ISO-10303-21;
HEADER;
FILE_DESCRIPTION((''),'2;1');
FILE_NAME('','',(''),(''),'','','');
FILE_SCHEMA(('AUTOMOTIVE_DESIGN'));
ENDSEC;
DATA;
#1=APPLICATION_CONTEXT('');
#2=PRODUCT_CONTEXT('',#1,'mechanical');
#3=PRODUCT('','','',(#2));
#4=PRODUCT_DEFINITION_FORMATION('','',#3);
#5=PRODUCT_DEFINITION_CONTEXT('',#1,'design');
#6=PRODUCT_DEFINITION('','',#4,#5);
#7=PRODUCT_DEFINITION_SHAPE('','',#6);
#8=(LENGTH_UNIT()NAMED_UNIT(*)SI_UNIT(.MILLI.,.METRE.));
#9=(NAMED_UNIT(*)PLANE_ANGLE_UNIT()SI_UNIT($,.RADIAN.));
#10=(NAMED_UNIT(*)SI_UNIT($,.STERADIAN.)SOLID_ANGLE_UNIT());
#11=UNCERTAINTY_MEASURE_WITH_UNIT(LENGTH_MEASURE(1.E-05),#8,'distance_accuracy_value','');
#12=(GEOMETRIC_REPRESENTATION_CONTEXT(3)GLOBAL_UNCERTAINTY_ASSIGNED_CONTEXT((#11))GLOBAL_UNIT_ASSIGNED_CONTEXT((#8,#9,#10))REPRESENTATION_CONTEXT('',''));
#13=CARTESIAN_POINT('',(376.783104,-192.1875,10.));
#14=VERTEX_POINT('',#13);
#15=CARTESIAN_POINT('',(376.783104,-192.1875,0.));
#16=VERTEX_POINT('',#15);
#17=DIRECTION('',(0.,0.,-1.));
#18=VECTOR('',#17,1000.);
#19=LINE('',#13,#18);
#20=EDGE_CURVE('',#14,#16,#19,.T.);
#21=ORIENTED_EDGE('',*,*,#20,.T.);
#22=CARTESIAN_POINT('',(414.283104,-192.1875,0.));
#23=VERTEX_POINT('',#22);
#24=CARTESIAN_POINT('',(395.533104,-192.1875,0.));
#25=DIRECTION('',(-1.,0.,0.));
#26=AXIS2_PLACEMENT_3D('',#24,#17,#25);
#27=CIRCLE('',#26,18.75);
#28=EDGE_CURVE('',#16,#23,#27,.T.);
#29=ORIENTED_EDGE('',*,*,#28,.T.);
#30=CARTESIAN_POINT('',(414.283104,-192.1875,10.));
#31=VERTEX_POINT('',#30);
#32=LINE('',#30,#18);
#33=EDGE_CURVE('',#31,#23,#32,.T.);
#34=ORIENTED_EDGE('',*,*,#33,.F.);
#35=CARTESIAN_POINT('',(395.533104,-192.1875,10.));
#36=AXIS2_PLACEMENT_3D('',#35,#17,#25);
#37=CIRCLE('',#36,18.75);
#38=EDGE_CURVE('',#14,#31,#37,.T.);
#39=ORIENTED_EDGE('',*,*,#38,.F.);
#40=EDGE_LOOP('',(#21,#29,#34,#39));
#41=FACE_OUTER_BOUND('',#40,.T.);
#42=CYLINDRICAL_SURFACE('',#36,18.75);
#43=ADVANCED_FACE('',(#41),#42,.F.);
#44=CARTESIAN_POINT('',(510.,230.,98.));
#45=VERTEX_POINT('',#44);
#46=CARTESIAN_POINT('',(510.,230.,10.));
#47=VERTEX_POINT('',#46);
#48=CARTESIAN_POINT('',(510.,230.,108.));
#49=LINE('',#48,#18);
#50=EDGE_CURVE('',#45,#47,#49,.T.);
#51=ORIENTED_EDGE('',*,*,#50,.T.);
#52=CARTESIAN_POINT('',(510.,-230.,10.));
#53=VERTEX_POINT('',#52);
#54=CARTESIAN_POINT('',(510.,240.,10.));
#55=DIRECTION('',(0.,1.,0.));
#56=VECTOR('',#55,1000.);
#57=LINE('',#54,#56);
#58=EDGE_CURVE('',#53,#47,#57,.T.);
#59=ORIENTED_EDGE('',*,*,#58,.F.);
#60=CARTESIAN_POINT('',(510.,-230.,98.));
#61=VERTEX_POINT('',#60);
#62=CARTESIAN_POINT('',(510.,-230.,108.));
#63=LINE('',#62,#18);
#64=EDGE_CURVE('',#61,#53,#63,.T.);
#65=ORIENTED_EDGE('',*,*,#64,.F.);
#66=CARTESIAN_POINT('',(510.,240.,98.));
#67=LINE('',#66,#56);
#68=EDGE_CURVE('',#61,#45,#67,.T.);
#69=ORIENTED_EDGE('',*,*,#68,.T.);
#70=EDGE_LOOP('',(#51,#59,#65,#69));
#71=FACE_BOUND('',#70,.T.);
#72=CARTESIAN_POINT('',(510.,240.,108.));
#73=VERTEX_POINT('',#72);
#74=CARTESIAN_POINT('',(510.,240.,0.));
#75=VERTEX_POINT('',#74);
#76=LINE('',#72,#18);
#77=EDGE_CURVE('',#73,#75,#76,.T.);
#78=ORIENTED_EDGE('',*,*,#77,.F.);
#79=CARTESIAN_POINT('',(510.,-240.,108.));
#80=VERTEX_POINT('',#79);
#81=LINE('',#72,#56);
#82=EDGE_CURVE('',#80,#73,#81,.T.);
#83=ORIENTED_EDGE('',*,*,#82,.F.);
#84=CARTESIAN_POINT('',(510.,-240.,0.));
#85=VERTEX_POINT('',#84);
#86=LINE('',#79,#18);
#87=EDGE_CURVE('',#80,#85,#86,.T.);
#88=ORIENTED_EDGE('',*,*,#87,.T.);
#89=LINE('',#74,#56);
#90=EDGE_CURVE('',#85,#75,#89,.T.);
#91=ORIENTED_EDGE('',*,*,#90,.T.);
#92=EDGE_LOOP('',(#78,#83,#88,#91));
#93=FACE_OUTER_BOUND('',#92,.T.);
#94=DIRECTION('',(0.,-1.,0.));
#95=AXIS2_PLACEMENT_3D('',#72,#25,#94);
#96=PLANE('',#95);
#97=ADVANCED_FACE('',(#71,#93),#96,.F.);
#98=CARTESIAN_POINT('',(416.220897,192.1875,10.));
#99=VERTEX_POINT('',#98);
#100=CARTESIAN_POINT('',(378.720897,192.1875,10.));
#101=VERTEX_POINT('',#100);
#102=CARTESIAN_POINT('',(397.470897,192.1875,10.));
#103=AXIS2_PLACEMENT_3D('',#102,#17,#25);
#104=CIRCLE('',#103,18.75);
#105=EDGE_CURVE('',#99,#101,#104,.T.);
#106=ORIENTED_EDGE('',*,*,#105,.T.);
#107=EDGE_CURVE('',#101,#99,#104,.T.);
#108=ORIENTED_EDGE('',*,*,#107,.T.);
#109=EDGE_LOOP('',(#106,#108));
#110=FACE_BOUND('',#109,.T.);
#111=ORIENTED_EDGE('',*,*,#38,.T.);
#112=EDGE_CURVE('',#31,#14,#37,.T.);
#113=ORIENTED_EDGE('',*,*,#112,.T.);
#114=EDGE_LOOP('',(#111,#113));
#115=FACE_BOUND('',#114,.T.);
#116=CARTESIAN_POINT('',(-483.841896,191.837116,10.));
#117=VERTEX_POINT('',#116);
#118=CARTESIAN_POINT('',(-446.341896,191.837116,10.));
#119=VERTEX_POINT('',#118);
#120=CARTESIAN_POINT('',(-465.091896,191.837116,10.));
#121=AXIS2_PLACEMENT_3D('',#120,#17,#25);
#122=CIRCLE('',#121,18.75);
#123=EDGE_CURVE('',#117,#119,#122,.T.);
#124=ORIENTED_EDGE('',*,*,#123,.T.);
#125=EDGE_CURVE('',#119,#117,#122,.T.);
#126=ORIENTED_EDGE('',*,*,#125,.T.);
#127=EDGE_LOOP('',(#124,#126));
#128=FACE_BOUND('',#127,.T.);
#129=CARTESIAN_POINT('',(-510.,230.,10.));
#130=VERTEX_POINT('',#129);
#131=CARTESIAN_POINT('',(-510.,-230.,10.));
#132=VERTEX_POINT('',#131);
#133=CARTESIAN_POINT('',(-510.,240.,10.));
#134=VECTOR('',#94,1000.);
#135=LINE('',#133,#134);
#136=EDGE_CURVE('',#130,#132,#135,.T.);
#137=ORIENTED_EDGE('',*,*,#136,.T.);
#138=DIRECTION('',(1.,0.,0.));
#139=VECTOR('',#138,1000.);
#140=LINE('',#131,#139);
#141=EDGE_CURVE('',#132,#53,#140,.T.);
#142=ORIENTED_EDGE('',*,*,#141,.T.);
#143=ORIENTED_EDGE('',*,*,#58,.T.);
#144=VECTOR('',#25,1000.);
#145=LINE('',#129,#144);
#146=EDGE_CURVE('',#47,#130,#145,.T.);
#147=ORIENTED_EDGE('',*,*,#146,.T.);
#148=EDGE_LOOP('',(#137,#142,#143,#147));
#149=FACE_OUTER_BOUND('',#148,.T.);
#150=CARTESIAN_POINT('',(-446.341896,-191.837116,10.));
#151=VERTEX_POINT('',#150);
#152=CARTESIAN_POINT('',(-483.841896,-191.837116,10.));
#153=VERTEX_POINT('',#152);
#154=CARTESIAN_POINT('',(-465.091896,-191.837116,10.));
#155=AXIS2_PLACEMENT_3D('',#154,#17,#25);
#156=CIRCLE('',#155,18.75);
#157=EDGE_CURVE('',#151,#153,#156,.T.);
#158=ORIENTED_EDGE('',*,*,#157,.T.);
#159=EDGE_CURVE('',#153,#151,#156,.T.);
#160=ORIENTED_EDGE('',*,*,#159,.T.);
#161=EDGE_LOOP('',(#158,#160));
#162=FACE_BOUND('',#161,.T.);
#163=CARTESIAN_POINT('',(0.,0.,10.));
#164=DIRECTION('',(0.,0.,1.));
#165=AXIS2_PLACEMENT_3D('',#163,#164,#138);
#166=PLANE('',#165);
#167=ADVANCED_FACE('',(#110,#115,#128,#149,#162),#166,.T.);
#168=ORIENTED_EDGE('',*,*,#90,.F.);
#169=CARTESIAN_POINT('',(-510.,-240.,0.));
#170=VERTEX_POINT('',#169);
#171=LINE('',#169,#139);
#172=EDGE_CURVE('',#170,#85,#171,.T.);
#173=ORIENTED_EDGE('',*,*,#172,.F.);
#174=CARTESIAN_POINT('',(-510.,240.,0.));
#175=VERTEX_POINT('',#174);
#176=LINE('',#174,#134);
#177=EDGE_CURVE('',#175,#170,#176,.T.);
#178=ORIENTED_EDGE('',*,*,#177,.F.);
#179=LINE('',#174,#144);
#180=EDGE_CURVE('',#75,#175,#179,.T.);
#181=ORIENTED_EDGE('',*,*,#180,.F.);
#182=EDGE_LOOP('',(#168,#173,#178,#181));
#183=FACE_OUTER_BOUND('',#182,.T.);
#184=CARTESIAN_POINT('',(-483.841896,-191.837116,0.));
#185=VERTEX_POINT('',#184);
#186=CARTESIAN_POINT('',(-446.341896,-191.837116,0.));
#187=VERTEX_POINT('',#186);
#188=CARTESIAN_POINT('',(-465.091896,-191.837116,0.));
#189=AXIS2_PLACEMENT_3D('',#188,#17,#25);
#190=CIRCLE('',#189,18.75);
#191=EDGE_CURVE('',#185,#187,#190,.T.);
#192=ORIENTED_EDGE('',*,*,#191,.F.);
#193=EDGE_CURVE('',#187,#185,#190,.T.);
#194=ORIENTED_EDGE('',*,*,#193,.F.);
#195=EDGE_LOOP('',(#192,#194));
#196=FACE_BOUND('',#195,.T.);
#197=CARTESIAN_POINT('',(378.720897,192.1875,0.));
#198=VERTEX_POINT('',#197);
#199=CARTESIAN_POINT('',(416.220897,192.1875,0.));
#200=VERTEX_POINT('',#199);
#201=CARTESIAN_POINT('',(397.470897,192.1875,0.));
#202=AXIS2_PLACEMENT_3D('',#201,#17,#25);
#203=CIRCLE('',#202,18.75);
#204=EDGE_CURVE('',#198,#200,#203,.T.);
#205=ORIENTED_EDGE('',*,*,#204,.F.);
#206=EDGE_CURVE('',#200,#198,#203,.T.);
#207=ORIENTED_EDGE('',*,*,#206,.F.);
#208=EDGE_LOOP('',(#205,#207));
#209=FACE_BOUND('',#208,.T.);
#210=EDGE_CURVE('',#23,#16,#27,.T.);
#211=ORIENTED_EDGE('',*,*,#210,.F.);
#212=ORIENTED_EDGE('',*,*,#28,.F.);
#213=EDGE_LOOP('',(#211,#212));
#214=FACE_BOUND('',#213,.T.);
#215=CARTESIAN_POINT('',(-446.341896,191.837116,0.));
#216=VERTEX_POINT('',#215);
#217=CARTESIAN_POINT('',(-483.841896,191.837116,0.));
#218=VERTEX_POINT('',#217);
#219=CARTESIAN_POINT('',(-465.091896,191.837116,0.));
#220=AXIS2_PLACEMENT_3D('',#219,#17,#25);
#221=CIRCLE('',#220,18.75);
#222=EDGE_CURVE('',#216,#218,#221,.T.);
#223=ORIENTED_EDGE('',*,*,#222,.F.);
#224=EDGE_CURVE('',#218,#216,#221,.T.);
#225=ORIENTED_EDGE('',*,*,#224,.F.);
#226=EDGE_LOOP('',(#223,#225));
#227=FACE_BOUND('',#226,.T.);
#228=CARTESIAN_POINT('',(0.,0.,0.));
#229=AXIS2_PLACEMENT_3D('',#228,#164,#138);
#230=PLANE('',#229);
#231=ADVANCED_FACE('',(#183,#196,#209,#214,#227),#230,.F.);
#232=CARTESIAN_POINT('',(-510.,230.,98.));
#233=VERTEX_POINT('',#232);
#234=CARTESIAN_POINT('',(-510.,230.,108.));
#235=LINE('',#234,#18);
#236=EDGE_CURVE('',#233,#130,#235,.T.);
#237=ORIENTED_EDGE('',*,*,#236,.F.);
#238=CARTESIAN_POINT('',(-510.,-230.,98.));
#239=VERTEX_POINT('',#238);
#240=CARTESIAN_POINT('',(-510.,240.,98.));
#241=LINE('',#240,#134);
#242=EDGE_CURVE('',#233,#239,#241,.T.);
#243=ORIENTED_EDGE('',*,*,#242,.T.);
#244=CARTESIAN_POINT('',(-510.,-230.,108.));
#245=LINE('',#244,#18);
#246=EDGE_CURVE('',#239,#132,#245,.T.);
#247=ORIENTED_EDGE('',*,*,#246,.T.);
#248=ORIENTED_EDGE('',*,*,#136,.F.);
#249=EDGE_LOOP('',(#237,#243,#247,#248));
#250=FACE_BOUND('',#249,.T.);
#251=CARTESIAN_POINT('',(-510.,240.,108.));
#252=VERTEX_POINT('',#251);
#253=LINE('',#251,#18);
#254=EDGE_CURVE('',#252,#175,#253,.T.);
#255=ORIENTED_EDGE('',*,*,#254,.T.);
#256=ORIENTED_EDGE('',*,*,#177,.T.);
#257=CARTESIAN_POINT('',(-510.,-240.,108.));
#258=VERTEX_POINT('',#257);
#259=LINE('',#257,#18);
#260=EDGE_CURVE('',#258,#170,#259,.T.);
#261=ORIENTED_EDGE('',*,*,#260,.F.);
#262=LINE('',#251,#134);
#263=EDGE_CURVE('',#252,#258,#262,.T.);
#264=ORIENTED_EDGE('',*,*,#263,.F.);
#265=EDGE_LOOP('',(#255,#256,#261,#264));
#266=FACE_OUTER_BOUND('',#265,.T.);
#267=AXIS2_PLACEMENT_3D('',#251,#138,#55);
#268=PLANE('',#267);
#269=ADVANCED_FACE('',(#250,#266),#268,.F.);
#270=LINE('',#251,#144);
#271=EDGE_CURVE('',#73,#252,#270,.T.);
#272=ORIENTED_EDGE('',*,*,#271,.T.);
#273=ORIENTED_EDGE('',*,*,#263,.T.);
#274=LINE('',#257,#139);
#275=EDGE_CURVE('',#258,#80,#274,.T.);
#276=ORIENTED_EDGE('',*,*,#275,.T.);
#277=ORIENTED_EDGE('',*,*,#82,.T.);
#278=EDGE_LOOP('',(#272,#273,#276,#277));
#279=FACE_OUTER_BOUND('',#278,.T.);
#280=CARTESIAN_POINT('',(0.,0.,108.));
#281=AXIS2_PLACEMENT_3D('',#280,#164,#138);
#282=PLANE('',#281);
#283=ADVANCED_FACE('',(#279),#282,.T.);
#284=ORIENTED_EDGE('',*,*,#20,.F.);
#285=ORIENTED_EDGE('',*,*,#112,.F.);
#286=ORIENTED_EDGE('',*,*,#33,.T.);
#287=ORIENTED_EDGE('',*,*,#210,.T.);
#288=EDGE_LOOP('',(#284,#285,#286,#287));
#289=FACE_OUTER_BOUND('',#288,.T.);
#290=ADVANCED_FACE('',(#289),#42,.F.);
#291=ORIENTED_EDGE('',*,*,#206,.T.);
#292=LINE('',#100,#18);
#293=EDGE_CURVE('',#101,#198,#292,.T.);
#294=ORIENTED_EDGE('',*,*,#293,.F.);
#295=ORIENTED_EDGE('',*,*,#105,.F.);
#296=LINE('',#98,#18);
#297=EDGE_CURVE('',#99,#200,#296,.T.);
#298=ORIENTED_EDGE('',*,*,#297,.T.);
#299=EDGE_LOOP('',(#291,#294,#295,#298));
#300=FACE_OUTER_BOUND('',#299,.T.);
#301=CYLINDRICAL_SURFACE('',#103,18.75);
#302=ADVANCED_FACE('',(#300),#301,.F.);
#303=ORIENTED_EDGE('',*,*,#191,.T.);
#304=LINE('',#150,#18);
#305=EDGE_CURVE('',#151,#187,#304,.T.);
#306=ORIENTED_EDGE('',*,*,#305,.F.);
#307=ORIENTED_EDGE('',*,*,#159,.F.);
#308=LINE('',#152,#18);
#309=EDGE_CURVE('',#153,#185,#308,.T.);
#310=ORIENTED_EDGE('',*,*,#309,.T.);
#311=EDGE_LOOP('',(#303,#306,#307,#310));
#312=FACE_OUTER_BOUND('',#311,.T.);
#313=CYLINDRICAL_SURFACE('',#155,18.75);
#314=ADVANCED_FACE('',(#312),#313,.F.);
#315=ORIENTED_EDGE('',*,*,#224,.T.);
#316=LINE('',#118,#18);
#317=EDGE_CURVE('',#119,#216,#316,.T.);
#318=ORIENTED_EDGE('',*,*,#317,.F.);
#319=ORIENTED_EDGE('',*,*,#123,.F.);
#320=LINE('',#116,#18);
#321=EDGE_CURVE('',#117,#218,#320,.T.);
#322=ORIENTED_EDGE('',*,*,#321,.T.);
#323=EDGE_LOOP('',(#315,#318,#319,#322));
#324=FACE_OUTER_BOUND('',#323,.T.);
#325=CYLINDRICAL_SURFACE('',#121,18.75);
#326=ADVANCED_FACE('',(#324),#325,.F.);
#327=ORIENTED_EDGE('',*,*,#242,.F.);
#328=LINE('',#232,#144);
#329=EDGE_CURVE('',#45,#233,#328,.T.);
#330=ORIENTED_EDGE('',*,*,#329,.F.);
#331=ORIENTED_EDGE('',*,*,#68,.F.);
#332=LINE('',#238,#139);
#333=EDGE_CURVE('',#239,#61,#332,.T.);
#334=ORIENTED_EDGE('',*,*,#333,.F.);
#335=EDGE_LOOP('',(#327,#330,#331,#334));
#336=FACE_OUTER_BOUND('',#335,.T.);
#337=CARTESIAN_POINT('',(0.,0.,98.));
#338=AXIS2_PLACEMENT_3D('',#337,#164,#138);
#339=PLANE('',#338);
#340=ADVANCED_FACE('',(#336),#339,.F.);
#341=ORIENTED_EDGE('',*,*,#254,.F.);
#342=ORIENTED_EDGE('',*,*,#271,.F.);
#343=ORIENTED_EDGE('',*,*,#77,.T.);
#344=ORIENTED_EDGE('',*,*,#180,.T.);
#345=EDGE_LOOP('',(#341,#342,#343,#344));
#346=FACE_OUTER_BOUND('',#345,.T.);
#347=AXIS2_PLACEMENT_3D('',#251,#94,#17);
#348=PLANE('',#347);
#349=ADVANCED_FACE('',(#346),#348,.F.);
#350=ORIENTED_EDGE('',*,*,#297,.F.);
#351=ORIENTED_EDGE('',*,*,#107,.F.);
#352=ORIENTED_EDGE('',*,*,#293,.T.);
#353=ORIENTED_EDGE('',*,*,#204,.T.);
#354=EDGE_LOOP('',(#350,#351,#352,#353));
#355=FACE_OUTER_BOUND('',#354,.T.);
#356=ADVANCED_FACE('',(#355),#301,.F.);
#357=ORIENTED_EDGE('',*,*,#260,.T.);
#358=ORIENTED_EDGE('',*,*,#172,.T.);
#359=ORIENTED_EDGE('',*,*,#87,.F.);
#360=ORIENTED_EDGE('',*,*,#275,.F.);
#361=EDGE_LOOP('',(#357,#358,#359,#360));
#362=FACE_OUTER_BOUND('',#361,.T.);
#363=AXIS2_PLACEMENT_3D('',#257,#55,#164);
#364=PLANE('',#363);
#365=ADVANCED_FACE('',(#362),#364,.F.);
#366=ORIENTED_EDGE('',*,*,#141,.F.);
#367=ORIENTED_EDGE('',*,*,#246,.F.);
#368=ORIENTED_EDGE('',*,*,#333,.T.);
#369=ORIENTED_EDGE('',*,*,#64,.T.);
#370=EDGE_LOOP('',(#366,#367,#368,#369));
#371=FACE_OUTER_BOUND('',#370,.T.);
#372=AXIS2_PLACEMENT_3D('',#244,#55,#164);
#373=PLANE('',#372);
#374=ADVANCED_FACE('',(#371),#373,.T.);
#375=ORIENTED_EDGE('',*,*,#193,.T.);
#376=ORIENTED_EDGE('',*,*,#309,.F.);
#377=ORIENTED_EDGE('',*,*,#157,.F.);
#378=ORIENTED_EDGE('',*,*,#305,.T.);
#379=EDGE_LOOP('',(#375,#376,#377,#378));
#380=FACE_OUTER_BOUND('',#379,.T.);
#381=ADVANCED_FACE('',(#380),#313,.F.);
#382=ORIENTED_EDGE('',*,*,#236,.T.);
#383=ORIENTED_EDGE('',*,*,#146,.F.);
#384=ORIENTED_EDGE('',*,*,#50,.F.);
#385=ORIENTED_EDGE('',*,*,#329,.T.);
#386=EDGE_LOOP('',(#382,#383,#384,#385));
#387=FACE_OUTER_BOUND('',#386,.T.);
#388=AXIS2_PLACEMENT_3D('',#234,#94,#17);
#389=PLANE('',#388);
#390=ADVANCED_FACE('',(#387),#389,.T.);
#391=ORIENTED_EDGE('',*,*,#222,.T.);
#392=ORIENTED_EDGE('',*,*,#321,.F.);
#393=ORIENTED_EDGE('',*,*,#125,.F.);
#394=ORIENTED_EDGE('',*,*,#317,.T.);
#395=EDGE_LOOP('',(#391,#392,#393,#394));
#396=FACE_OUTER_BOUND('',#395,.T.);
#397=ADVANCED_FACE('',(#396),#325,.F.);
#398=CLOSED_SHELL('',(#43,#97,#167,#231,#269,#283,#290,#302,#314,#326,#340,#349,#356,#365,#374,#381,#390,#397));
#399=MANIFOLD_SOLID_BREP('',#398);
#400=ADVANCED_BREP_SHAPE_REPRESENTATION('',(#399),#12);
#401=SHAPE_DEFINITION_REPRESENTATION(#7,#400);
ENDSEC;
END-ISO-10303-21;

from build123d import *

# Parameters (mm, degrees)
SKETCH1_W           = 1020
SKETCH1_H           = 480
BOSS_EXTRUDE1_DEPTH = 108
SHELL1_T            = -10
SKETCH2_R           = 18.75
CUT_EXTRUDE1_DEPTH  = 10


with BuildPart() as part:
    # Sketch1 → Boss-Extrude1 (new body)
    with BuildSketch(Plane.XY):
        Rectangle(SKETCH1_W, SKETCH1_H)
    extrude(amount=BOSS_EXTRUDE1_DEPTH)

    # Shell1
    shell1_openings = [part.faces().sort_by_distance(p)[0] for p in [
        (-510, 0, 54),
        (510, 0, 54),
    ]]
    offset(amount=SHELL1_T, openings=shell1_openings, kind=Kind.INTERSECTION)

    # Sketch2 → Cut-Extrude1 (cut)
    with BuildSketch(Plane(origin=(0, 0, 0), x_dir=(-1, 0, 0), z_dir=(0, 0, -1))):
        with Locations((-397.470896816, 192.1875)):
            Circle(SKETCH2_R)
        with Locations((-395.533103518, -192.1875)):
            Circle(SKETCH2_R)
        with Locations((465.091896482, -191.83711567)):
            Circle(SKETCH2_R)
        with Locations((465.091896482, 191.83711567)):
            Circle(SKETCH2_R)
    extrude(amount=-CUT_EXTRUDE1_DEPTH, mode=Mode.SUBTRACT)


solid = part.part
